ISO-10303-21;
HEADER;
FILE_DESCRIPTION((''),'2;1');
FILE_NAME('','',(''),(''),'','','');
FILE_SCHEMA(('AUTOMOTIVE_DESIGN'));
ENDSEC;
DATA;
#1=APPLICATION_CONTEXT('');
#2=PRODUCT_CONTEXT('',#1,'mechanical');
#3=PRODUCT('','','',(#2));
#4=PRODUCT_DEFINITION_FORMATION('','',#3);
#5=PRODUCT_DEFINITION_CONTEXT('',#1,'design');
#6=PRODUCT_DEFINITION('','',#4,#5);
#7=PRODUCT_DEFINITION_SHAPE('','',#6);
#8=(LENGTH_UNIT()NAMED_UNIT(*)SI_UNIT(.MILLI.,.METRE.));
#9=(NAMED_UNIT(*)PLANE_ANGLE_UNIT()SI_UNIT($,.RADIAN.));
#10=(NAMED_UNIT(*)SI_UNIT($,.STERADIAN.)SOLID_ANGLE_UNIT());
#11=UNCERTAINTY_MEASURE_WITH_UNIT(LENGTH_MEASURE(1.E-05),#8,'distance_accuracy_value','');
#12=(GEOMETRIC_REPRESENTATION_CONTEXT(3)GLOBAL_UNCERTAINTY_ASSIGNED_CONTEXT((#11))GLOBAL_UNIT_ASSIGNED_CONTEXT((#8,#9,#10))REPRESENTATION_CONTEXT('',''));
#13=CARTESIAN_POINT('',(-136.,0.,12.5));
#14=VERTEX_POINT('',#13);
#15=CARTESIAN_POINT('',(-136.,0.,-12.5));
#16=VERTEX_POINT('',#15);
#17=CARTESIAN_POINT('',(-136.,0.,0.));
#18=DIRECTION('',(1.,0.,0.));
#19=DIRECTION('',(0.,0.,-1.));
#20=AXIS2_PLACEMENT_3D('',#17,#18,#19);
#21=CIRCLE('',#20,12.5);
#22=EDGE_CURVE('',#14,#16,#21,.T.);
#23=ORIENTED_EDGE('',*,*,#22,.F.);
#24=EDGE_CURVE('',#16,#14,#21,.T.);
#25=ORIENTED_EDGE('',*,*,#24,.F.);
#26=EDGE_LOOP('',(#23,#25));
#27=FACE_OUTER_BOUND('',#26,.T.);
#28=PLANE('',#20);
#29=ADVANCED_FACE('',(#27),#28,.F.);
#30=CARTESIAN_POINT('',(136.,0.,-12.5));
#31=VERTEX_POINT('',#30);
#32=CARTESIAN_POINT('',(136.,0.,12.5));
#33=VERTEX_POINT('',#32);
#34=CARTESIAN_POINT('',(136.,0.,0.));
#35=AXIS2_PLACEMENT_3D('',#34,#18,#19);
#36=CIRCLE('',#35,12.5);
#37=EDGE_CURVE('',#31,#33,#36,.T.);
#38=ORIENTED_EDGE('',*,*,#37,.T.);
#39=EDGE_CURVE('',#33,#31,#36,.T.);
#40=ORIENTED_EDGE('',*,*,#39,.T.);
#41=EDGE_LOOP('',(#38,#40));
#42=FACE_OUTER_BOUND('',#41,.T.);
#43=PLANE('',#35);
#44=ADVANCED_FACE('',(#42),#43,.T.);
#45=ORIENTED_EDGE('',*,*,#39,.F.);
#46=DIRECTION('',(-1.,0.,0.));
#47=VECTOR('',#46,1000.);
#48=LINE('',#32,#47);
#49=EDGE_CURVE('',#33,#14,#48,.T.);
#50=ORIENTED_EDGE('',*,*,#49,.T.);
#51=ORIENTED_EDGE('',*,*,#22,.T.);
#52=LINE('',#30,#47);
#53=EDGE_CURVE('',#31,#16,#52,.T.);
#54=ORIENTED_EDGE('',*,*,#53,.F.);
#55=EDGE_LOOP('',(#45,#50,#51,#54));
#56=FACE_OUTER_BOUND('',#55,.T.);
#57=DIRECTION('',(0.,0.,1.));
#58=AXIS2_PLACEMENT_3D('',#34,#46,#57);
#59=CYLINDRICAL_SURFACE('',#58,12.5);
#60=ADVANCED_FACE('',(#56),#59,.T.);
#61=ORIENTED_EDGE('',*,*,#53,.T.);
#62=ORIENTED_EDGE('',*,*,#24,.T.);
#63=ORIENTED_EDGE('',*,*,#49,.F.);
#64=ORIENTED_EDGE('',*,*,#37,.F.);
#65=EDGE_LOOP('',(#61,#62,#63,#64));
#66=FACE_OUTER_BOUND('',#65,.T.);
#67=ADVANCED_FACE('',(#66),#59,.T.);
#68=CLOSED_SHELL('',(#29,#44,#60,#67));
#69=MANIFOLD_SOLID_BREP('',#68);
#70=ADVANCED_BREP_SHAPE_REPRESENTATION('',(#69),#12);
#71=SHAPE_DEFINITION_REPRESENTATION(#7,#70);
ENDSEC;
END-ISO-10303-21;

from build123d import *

# Parameters (mm, degrees)
SKETCH_1_R      = 12.5
EXTRUDE_1_DEPTH = 136


with BuildPart() as part:
    # 草图1 → 凸台-拉伸1 (new, symmetric)
    with BuildSketch(Plane(origin=(0, 0, 0), x_dir=(0, 0, -1), z_dir=(1, 0, 0))):
        Circle(SKETCH_1_R)
    extrude(amount=EXTRUDE_1_DEPTH, both=True)


solid = part.part
